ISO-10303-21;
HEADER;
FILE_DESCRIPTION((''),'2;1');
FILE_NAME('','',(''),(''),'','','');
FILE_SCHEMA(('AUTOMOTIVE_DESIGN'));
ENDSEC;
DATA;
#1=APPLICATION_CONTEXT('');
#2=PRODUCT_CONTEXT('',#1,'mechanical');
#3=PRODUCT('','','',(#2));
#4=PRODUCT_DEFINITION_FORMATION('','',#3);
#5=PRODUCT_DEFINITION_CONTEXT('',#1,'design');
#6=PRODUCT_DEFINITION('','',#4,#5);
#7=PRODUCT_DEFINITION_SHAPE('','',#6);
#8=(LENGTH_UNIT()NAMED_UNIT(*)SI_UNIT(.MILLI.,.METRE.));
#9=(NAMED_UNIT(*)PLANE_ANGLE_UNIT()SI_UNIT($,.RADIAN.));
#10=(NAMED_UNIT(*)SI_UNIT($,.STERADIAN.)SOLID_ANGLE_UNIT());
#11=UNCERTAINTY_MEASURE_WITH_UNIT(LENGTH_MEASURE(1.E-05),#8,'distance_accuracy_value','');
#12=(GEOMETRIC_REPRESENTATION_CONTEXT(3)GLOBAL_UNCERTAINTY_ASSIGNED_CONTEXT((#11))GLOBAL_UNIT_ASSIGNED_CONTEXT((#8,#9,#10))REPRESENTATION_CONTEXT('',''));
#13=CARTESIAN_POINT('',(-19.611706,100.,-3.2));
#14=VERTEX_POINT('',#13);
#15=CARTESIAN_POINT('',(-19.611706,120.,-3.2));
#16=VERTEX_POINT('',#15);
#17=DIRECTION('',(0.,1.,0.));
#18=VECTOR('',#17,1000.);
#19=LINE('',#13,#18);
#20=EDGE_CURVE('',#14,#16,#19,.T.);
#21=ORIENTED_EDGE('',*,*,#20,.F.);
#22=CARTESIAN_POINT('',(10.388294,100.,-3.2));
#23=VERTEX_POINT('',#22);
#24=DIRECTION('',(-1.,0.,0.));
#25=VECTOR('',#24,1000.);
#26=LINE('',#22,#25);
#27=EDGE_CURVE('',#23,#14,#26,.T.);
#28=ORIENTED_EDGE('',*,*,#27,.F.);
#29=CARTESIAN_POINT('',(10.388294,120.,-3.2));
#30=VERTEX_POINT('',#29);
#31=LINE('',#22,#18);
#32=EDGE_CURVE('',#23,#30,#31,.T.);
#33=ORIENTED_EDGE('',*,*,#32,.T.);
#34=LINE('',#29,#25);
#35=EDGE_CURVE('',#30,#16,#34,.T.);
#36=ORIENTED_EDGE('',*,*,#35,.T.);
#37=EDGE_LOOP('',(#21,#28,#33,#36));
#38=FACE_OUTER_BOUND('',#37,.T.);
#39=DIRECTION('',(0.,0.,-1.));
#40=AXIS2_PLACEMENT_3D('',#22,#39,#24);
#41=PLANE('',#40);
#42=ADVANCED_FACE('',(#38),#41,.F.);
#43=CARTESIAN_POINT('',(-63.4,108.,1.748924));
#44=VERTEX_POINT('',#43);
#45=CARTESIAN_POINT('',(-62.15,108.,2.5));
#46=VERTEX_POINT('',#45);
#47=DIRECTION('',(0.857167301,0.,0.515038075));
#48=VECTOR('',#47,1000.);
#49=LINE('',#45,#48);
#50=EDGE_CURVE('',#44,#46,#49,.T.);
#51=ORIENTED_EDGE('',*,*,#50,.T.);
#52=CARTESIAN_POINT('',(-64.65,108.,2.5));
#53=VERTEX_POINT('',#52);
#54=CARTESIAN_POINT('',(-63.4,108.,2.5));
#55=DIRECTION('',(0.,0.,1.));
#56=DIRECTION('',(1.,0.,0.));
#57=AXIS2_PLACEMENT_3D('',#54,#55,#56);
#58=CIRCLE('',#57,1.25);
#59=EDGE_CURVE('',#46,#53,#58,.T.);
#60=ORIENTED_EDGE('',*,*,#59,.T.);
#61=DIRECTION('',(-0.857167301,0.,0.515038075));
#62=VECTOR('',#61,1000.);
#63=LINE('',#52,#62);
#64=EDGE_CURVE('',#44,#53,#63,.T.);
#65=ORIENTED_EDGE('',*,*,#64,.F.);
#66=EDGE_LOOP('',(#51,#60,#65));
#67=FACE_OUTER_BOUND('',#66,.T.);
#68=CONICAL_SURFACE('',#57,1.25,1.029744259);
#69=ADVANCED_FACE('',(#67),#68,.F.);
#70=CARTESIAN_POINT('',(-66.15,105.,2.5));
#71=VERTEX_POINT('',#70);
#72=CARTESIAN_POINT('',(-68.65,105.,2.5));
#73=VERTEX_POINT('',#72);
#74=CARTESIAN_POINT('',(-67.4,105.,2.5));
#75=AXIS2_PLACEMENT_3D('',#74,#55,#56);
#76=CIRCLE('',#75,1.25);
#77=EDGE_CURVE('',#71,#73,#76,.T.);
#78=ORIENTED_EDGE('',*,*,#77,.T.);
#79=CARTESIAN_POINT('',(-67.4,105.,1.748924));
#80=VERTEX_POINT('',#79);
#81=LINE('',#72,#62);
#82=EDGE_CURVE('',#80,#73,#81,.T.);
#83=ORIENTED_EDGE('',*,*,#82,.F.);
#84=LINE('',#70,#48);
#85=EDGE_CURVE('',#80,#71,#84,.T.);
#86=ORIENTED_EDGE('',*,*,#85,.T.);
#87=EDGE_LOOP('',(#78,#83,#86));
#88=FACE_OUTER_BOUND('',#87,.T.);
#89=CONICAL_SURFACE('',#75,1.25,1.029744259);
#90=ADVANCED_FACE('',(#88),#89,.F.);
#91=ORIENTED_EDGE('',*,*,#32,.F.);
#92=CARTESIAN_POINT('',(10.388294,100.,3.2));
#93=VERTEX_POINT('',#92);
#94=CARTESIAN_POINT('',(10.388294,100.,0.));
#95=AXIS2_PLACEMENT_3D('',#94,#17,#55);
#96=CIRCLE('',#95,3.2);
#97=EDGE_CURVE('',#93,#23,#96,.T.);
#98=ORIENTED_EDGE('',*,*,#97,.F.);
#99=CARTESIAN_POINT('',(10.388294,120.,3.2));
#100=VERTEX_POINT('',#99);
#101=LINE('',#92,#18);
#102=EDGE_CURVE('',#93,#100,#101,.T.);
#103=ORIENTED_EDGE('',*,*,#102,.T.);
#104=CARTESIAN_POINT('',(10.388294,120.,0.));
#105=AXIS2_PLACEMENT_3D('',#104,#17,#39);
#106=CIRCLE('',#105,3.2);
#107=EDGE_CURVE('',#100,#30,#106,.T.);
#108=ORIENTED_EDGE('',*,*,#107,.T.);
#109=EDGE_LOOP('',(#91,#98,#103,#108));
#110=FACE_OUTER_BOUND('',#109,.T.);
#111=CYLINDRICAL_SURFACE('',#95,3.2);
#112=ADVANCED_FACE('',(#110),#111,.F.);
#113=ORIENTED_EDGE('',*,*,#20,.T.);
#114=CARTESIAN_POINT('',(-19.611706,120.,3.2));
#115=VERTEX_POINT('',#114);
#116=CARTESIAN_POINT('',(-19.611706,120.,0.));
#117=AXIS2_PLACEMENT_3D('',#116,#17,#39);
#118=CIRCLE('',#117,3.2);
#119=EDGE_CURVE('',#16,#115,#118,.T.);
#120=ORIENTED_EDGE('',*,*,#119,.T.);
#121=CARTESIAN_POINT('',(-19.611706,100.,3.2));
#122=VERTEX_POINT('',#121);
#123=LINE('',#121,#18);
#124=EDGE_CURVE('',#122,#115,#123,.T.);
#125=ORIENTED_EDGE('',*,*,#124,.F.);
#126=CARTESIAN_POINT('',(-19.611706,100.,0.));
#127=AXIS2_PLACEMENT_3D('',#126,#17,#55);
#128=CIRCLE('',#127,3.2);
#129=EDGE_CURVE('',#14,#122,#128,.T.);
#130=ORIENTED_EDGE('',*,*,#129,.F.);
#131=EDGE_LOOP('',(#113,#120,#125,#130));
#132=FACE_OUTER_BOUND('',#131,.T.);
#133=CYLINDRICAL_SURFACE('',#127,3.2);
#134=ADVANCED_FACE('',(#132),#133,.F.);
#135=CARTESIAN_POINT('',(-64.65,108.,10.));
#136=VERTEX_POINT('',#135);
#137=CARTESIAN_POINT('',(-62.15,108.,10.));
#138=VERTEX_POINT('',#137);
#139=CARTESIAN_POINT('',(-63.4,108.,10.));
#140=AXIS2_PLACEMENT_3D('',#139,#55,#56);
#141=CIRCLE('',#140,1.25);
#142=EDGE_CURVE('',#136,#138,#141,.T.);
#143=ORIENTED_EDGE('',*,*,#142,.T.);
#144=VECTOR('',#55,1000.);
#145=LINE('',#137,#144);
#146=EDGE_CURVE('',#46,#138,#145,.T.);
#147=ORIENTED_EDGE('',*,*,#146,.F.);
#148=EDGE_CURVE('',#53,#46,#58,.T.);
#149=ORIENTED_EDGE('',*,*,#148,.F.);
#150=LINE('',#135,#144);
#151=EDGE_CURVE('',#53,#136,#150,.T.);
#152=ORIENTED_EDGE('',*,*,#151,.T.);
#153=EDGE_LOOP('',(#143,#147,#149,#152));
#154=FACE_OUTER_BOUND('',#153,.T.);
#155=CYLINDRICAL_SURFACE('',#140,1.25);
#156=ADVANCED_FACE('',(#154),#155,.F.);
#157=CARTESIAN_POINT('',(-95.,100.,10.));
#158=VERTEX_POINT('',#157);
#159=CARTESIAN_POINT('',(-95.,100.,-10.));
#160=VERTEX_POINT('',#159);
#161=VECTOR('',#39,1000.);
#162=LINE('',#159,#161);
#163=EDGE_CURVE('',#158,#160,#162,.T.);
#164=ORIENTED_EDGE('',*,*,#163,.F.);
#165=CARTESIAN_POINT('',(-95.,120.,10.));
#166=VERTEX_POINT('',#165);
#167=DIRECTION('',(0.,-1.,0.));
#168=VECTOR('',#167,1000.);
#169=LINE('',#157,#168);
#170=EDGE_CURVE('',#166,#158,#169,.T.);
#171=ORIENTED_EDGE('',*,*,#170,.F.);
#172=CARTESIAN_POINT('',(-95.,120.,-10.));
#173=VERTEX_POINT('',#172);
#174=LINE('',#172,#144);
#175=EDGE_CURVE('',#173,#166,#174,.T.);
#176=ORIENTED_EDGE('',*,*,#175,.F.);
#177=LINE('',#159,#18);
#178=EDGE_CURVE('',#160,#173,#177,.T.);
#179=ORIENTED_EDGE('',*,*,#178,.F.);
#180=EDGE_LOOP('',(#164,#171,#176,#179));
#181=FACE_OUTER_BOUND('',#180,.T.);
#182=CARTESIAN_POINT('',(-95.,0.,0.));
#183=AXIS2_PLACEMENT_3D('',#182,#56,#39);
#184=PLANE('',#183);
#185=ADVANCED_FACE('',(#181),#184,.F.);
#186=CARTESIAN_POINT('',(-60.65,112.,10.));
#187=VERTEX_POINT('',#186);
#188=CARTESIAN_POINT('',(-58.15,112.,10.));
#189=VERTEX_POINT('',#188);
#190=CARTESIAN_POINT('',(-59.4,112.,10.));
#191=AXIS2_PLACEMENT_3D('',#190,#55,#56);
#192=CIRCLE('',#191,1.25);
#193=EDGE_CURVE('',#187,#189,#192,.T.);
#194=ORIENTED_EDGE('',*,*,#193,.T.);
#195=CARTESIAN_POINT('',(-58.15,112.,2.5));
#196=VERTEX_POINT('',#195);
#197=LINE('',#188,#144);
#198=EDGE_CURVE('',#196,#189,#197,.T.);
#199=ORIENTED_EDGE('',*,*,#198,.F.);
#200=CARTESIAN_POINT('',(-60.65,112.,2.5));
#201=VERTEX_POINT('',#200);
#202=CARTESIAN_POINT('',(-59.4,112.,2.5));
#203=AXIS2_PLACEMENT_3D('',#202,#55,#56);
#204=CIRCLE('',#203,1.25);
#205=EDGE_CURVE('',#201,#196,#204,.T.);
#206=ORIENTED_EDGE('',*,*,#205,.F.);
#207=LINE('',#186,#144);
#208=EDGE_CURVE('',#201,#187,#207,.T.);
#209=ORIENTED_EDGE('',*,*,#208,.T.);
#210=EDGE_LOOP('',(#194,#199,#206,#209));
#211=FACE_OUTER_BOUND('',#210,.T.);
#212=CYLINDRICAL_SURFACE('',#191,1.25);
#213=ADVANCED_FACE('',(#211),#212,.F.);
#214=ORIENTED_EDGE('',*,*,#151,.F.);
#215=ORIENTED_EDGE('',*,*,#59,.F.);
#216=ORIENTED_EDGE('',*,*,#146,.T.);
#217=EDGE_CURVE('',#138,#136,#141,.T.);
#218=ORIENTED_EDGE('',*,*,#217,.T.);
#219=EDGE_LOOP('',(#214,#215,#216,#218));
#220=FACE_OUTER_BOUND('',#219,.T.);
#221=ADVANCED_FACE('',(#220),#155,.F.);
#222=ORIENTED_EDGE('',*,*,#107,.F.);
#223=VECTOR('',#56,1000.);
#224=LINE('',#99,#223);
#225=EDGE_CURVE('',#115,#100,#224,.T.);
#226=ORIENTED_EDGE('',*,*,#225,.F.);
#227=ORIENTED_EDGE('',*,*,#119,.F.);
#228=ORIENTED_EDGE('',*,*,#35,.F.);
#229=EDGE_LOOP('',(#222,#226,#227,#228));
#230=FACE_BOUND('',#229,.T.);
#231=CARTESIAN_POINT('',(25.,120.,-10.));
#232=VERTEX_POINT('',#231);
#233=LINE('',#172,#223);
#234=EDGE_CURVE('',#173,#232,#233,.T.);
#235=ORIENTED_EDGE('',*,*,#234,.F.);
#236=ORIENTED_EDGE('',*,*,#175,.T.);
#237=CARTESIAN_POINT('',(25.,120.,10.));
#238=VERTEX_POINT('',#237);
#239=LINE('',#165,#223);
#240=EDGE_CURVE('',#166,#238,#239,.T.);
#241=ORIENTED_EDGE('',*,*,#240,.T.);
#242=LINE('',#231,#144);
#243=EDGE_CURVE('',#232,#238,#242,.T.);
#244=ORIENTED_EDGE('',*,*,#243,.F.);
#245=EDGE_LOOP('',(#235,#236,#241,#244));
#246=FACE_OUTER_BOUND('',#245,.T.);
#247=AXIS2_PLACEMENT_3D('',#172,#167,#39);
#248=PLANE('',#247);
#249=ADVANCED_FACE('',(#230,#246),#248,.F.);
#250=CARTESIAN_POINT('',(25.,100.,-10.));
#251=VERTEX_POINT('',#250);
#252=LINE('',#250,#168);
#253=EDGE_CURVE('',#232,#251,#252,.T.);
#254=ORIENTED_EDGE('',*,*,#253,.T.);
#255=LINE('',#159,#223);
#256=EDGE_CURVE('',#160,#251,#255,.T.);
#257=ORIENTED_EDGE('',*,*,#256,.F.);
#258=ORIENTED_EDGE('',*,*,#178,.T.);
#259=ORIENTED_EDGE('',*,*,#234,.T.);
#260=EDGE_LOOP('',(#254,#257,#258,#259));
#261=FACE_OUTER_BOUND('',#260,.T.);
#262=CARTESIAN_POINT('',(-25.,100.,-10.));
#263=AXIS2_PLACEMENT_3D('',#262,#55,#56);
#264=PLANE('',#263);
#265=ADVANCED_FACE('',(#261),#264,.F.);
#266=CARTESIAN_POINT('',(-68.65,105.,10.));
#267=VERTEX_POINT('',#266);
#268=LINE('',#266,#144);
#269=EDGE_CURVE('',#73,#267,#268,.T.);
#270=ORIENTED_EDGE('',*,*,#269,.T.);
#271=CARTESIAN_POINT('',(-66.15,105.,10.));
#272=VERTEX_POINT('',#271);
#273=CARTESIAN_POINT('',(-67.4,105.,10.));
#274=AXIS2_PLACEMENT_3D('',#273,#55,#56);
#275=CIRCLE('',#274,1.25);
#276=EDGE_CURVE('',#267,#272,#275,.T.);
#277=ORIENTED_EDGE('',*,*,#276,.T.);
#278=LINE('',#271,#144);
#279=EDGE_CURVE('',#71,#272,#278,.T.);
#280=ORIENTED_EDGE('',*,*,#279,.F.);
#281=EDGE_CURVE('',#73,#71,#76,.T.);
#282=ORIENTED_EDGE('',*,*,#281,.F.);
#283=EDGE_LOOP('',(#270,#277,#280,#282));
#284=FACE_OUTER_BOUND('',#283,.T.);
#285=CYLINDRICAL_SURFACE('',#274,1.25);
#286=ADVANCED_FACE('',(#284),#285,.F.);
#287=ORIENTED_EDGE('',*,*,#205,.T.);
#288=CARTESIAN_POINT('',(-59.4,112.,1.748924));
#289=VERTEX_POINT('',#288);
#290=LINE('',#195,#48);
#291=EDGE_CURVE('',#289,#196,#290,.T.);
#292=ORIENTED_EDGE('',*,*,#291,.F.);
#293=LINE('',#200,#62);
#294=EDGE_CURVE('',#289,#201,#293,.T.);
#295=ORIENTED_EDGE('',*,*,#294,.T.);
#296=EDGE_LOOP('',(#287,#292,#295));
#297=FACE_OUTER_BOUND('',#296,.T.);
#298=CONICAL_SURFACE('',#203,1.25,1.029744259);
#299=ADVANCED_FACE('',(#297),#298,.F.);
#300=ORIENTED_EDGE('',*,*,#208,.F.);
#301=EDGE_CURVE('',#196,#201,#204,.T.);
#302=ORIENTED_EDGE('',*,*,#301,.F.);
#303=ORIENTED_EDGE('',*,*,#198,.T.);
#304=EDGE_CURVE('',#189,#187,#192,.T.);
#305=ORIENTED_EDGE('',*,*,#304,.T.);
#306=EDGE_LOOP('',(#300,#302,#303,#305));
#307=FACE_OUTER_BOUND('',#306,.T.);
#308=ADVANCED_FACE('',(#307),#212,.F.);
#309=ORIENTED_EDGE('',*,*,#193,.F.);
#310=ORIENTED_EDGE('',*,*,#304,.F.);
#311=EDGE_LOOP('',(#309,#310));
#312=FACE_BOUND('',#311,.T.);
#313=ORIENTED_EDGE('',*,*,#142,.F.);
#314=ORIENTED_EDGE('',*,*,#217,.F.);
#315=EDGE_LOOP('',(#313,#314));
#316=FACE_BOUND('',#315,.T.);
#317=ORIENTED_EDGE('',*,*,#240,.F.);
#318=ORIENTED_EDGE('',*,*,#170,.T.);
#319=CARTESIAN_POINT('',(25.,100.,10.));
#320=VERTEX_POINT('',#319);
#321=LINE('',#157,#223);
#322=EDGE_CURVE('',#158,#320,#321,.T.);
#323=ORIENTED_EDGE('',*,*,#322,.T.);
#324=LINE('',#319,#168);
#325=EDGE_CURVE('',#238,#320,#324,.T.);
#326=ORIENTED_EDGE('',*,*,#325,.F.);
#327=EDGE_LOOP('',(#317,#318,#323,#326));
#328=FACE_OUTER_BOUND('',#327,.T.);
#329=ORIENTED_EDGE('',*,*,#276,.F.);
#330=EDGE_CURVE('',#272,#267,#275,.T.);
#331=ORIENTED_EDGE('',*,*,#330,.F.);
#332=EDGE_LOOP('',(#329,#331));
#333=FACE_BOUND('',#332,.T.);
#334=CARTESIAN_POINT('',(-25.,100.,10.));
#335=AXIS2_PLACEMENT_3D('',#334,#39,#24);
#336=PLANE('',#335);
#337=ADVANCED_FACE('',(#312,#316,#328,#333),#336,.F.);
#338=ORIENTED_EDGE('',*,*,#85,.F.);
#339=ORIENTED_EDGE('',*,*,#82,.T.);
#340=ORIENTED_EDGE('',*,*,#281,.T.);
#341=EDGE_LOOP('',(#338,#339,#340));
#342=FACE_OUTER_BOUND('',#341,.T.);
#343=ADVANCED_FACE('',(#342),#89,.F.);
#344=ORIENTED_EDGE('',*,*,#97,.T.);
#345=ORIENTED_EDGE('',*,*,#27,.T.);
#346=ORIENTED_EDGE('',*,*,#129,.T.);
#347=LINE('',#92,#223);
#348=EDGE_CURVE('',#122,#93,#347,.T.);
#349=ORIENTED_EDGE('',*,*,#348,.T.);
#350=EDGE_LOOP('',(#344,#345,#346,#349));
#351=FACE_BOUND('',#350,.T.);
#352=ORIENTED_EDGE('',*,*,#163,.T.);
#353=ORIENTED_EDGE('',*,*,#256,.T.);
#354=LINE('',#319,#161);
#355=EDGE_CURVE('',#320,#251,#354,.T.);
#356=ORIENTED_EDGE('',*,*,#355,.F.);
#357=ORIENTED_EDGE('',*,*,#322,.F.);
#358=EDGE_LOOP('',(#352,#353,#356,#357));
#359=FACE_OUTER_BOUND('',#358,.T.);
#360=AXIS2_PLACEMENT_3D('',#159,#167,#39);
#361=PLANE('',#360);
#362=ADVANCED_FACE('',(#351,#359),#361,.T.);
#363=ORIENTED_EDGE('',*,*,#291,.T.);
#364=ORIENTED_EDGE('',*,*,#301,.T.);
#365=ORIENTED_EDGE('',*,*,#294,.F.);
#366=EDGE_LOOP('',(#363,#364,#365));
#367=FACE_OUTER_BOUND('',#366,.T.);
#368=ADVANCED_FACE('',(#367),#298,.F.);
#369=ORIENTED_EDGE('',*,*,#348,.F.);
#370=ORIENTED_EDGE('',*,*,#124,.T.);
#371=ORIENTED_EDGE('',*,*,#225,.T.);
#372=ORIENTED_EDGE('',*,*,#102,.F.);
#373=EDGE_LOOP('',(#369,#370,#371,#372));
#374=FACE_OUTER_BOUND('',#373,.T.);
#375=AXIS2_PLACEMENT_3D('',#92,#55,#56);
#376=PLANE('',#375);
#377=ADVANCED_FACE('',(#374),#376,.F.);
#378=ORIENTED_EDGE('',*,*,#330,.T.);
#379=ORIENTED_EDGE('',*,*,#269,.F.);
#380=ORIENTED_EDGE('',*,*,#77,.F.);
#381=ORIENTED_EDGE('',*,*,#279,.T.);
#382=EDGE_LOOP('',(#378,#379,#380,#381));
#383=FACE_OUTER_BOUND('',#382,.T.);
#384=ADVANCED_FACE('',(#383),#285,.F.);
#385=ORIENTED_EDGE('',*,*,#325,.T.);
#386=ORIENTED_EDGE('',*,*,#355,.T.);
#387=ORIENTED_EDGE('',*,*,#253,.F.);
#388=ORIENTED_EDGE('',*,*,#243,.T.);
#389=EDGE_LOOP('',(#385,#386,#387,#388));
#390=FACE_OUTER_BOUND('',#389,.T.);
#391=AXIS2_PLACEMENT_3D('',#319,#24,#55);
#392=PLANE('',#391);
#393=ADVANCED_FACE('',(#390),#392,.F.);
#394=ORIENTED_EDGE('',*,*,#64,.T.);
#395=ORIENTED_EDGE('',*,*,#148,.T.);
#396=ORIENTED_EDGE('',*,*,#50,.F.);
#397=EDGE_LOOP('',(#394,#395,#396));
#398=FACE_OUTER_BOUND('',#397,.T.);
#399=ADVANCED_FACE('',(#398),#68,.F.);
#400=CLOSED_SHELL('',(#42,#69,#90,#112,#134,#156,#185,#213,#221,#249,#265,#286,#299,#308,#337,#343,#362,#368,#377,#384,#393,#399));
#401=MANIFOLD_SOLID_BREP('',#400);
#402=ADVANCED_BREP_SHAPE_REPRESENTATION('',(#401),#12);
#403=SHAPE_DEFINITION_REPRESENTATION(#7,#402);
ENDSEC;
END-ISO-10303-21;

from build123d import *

# Parameters (mm, degrees)
SKETCH1_W             = 50
SKETCH1_H             = 20
BOSS_EXTRUDE1_DEPTH   = 100
SKETCH2_R             = 3
BOSS_EXTRUDE2_DEPTH   = 5
M6_TAPPED_HOLE1_D     = 5
M6_TAPPED_HOLE1_DEPTH = 15
M6_TAPPED_HOLE1_TIP   = 1.502151548
SKETCH5_W             = 20
SKETCH5_H             = 30
BOSS_EXTRUDE3_DEPTH   = 120
M3_TAPPED_HOLE1_D     = 2.5
M3_TAPPED_HOLE1_DEPTH = 7.5
M3_TAPPED_HOLE1_TIP   = 0.751075774
SKETCH8_W             = 95.008103892
SKETCH8_H             = 183.237528091
CUT_EXTRUDE1_DEPTH    = 163.249807396
CUT_EXTRUDE2_DEPTH    = 101.124921973
SKETCH10_W            = 120
SKETCH10_H            = 10
CUT_EXTRUDE3_DEPTH    = 163.249807396


with BuildPart() as part:
    # Sketch1 → Boss-Extrude1 (new body)
    with BuildSketch(Plane(origin=(0, 0, 0), x_dir=(1, 0, 0), z_dir=(0, 1, 0))):
        Rectangle(SKETCH1_W, SKETCH1_H)
    extrude(amount=BOSS_EXTRUDE1_DEPTH)

    # Sketch2 → Boss-Extrude2 (add)
    with BuildSketch(Plane.XZ):
        with Locations(Location((0, 5, 0), (0, 0, 270))):
            Circle(SKETCH2_R)
    extrude(amount=BOSS_EXTRUDE2_DEPTH)

    # M6 Tapped Hole1
    with Locations(Plane(origin=(0, 0, 0), x_dir=(-1, 0, 0), z_dir=(0, -1, 0))):
        with Locations((0, 5)):
            Hole(M6_TAPPED_HOLE1_D / 2, depth=M6_TAPPED_HOLE1_DEPTH)
            with Locations((0, 0, -(M6_TAPPED_HOLE1_DEPTH + M6_TAPPED_HOLE1_TIP / 2))):  # 118° drill point
                Cone(0, M6_TAPPED_HOLE1_D / 2, M6_TAPPED_HOLE1_TIP, mode=Mode.SUBTRACT)

    # Sketch5 → Boss-Extrude3 (add)
    with BuildSketch(Plane(origin=(25, 0, 0), x_dir=(0, 0, -1), z_dir=(1, 0, 0))):
        with Locations((0, 115)):
            Rectangle(SKETCH5_W, SKETCH5_H)
    extrude(amount=-BOSS_EXTRUDE3_DEPTH)

    # M3 Tapped Hole1
    with Locations(Plane.XY.offset(10)):
        with Locations((-63.4, 108), (-59.4, 112), (-67.4, 105)):
            Hole(M3_TAPPED_HOLE1_D / 2, depth=M3_TAPPED_HOLE1_DEPTH)
            with Locations((0, 0, -(M3_TAPPED_HOLE1_DEPTH + M3_TAPPED_HOLE1_TIP / 2))):  # 118° drill point
                Cone(0, M3_TAPPED_HOLE1_D / 2, M3_TAPPED_HOLE1_TIP, mode=Mode.SUBTRACT)

    # Sketch8 → Cut-Extrude1 (cut, through all)
    with BuildSketch(Plane.XY.offset(10)):
        with Locations((22.504051946, 8.381235954)):
            Rectangle(SKETCH8_W, SKETCH8_H)
    extrude(amount=-CUT_EXTRUDE1_DEPTH, mode=Mode.SUBTRACT)

    # Sketch9 → Cut-Extrude2 (cut, through all)
    with BuildSketch(Plane(origin=(0, 130, 0), x_dir=(1, 0, 0), z_dir=(0, 1, 0))):
        with BuildLine():
            Line((10.388294344, -3.2), (-19.611705656, -3.2))
            ThreePointArc((-19.611705656, -3.2), (-22.811705656, 0), (-19.611705656, 3.2))
            Line((-19.611705656, 3.2), (10.388294344, 3.2))
            ThreePointArc((10.388294344, 3.2), (13.588294344, 0), (10.388294344, -3.2))
        make_face()
    extrude(amount=-CUT_EXTRUDE2_DEPTH, mode=Mode.SUBTRACT)

    # Sketch10 → Cut-Extrude3 (cut, through all)
    with BuildSketch(Plane.XY.offset(10)):
        with Locations((-35, 125)):
            Rectangle(SKETCH10_W, SKETCH10_H)
    extrude(amount=-CUT_EXTRUDE3_DEPTH, mode=Mode.SUBTRACT)


solid = part.part
